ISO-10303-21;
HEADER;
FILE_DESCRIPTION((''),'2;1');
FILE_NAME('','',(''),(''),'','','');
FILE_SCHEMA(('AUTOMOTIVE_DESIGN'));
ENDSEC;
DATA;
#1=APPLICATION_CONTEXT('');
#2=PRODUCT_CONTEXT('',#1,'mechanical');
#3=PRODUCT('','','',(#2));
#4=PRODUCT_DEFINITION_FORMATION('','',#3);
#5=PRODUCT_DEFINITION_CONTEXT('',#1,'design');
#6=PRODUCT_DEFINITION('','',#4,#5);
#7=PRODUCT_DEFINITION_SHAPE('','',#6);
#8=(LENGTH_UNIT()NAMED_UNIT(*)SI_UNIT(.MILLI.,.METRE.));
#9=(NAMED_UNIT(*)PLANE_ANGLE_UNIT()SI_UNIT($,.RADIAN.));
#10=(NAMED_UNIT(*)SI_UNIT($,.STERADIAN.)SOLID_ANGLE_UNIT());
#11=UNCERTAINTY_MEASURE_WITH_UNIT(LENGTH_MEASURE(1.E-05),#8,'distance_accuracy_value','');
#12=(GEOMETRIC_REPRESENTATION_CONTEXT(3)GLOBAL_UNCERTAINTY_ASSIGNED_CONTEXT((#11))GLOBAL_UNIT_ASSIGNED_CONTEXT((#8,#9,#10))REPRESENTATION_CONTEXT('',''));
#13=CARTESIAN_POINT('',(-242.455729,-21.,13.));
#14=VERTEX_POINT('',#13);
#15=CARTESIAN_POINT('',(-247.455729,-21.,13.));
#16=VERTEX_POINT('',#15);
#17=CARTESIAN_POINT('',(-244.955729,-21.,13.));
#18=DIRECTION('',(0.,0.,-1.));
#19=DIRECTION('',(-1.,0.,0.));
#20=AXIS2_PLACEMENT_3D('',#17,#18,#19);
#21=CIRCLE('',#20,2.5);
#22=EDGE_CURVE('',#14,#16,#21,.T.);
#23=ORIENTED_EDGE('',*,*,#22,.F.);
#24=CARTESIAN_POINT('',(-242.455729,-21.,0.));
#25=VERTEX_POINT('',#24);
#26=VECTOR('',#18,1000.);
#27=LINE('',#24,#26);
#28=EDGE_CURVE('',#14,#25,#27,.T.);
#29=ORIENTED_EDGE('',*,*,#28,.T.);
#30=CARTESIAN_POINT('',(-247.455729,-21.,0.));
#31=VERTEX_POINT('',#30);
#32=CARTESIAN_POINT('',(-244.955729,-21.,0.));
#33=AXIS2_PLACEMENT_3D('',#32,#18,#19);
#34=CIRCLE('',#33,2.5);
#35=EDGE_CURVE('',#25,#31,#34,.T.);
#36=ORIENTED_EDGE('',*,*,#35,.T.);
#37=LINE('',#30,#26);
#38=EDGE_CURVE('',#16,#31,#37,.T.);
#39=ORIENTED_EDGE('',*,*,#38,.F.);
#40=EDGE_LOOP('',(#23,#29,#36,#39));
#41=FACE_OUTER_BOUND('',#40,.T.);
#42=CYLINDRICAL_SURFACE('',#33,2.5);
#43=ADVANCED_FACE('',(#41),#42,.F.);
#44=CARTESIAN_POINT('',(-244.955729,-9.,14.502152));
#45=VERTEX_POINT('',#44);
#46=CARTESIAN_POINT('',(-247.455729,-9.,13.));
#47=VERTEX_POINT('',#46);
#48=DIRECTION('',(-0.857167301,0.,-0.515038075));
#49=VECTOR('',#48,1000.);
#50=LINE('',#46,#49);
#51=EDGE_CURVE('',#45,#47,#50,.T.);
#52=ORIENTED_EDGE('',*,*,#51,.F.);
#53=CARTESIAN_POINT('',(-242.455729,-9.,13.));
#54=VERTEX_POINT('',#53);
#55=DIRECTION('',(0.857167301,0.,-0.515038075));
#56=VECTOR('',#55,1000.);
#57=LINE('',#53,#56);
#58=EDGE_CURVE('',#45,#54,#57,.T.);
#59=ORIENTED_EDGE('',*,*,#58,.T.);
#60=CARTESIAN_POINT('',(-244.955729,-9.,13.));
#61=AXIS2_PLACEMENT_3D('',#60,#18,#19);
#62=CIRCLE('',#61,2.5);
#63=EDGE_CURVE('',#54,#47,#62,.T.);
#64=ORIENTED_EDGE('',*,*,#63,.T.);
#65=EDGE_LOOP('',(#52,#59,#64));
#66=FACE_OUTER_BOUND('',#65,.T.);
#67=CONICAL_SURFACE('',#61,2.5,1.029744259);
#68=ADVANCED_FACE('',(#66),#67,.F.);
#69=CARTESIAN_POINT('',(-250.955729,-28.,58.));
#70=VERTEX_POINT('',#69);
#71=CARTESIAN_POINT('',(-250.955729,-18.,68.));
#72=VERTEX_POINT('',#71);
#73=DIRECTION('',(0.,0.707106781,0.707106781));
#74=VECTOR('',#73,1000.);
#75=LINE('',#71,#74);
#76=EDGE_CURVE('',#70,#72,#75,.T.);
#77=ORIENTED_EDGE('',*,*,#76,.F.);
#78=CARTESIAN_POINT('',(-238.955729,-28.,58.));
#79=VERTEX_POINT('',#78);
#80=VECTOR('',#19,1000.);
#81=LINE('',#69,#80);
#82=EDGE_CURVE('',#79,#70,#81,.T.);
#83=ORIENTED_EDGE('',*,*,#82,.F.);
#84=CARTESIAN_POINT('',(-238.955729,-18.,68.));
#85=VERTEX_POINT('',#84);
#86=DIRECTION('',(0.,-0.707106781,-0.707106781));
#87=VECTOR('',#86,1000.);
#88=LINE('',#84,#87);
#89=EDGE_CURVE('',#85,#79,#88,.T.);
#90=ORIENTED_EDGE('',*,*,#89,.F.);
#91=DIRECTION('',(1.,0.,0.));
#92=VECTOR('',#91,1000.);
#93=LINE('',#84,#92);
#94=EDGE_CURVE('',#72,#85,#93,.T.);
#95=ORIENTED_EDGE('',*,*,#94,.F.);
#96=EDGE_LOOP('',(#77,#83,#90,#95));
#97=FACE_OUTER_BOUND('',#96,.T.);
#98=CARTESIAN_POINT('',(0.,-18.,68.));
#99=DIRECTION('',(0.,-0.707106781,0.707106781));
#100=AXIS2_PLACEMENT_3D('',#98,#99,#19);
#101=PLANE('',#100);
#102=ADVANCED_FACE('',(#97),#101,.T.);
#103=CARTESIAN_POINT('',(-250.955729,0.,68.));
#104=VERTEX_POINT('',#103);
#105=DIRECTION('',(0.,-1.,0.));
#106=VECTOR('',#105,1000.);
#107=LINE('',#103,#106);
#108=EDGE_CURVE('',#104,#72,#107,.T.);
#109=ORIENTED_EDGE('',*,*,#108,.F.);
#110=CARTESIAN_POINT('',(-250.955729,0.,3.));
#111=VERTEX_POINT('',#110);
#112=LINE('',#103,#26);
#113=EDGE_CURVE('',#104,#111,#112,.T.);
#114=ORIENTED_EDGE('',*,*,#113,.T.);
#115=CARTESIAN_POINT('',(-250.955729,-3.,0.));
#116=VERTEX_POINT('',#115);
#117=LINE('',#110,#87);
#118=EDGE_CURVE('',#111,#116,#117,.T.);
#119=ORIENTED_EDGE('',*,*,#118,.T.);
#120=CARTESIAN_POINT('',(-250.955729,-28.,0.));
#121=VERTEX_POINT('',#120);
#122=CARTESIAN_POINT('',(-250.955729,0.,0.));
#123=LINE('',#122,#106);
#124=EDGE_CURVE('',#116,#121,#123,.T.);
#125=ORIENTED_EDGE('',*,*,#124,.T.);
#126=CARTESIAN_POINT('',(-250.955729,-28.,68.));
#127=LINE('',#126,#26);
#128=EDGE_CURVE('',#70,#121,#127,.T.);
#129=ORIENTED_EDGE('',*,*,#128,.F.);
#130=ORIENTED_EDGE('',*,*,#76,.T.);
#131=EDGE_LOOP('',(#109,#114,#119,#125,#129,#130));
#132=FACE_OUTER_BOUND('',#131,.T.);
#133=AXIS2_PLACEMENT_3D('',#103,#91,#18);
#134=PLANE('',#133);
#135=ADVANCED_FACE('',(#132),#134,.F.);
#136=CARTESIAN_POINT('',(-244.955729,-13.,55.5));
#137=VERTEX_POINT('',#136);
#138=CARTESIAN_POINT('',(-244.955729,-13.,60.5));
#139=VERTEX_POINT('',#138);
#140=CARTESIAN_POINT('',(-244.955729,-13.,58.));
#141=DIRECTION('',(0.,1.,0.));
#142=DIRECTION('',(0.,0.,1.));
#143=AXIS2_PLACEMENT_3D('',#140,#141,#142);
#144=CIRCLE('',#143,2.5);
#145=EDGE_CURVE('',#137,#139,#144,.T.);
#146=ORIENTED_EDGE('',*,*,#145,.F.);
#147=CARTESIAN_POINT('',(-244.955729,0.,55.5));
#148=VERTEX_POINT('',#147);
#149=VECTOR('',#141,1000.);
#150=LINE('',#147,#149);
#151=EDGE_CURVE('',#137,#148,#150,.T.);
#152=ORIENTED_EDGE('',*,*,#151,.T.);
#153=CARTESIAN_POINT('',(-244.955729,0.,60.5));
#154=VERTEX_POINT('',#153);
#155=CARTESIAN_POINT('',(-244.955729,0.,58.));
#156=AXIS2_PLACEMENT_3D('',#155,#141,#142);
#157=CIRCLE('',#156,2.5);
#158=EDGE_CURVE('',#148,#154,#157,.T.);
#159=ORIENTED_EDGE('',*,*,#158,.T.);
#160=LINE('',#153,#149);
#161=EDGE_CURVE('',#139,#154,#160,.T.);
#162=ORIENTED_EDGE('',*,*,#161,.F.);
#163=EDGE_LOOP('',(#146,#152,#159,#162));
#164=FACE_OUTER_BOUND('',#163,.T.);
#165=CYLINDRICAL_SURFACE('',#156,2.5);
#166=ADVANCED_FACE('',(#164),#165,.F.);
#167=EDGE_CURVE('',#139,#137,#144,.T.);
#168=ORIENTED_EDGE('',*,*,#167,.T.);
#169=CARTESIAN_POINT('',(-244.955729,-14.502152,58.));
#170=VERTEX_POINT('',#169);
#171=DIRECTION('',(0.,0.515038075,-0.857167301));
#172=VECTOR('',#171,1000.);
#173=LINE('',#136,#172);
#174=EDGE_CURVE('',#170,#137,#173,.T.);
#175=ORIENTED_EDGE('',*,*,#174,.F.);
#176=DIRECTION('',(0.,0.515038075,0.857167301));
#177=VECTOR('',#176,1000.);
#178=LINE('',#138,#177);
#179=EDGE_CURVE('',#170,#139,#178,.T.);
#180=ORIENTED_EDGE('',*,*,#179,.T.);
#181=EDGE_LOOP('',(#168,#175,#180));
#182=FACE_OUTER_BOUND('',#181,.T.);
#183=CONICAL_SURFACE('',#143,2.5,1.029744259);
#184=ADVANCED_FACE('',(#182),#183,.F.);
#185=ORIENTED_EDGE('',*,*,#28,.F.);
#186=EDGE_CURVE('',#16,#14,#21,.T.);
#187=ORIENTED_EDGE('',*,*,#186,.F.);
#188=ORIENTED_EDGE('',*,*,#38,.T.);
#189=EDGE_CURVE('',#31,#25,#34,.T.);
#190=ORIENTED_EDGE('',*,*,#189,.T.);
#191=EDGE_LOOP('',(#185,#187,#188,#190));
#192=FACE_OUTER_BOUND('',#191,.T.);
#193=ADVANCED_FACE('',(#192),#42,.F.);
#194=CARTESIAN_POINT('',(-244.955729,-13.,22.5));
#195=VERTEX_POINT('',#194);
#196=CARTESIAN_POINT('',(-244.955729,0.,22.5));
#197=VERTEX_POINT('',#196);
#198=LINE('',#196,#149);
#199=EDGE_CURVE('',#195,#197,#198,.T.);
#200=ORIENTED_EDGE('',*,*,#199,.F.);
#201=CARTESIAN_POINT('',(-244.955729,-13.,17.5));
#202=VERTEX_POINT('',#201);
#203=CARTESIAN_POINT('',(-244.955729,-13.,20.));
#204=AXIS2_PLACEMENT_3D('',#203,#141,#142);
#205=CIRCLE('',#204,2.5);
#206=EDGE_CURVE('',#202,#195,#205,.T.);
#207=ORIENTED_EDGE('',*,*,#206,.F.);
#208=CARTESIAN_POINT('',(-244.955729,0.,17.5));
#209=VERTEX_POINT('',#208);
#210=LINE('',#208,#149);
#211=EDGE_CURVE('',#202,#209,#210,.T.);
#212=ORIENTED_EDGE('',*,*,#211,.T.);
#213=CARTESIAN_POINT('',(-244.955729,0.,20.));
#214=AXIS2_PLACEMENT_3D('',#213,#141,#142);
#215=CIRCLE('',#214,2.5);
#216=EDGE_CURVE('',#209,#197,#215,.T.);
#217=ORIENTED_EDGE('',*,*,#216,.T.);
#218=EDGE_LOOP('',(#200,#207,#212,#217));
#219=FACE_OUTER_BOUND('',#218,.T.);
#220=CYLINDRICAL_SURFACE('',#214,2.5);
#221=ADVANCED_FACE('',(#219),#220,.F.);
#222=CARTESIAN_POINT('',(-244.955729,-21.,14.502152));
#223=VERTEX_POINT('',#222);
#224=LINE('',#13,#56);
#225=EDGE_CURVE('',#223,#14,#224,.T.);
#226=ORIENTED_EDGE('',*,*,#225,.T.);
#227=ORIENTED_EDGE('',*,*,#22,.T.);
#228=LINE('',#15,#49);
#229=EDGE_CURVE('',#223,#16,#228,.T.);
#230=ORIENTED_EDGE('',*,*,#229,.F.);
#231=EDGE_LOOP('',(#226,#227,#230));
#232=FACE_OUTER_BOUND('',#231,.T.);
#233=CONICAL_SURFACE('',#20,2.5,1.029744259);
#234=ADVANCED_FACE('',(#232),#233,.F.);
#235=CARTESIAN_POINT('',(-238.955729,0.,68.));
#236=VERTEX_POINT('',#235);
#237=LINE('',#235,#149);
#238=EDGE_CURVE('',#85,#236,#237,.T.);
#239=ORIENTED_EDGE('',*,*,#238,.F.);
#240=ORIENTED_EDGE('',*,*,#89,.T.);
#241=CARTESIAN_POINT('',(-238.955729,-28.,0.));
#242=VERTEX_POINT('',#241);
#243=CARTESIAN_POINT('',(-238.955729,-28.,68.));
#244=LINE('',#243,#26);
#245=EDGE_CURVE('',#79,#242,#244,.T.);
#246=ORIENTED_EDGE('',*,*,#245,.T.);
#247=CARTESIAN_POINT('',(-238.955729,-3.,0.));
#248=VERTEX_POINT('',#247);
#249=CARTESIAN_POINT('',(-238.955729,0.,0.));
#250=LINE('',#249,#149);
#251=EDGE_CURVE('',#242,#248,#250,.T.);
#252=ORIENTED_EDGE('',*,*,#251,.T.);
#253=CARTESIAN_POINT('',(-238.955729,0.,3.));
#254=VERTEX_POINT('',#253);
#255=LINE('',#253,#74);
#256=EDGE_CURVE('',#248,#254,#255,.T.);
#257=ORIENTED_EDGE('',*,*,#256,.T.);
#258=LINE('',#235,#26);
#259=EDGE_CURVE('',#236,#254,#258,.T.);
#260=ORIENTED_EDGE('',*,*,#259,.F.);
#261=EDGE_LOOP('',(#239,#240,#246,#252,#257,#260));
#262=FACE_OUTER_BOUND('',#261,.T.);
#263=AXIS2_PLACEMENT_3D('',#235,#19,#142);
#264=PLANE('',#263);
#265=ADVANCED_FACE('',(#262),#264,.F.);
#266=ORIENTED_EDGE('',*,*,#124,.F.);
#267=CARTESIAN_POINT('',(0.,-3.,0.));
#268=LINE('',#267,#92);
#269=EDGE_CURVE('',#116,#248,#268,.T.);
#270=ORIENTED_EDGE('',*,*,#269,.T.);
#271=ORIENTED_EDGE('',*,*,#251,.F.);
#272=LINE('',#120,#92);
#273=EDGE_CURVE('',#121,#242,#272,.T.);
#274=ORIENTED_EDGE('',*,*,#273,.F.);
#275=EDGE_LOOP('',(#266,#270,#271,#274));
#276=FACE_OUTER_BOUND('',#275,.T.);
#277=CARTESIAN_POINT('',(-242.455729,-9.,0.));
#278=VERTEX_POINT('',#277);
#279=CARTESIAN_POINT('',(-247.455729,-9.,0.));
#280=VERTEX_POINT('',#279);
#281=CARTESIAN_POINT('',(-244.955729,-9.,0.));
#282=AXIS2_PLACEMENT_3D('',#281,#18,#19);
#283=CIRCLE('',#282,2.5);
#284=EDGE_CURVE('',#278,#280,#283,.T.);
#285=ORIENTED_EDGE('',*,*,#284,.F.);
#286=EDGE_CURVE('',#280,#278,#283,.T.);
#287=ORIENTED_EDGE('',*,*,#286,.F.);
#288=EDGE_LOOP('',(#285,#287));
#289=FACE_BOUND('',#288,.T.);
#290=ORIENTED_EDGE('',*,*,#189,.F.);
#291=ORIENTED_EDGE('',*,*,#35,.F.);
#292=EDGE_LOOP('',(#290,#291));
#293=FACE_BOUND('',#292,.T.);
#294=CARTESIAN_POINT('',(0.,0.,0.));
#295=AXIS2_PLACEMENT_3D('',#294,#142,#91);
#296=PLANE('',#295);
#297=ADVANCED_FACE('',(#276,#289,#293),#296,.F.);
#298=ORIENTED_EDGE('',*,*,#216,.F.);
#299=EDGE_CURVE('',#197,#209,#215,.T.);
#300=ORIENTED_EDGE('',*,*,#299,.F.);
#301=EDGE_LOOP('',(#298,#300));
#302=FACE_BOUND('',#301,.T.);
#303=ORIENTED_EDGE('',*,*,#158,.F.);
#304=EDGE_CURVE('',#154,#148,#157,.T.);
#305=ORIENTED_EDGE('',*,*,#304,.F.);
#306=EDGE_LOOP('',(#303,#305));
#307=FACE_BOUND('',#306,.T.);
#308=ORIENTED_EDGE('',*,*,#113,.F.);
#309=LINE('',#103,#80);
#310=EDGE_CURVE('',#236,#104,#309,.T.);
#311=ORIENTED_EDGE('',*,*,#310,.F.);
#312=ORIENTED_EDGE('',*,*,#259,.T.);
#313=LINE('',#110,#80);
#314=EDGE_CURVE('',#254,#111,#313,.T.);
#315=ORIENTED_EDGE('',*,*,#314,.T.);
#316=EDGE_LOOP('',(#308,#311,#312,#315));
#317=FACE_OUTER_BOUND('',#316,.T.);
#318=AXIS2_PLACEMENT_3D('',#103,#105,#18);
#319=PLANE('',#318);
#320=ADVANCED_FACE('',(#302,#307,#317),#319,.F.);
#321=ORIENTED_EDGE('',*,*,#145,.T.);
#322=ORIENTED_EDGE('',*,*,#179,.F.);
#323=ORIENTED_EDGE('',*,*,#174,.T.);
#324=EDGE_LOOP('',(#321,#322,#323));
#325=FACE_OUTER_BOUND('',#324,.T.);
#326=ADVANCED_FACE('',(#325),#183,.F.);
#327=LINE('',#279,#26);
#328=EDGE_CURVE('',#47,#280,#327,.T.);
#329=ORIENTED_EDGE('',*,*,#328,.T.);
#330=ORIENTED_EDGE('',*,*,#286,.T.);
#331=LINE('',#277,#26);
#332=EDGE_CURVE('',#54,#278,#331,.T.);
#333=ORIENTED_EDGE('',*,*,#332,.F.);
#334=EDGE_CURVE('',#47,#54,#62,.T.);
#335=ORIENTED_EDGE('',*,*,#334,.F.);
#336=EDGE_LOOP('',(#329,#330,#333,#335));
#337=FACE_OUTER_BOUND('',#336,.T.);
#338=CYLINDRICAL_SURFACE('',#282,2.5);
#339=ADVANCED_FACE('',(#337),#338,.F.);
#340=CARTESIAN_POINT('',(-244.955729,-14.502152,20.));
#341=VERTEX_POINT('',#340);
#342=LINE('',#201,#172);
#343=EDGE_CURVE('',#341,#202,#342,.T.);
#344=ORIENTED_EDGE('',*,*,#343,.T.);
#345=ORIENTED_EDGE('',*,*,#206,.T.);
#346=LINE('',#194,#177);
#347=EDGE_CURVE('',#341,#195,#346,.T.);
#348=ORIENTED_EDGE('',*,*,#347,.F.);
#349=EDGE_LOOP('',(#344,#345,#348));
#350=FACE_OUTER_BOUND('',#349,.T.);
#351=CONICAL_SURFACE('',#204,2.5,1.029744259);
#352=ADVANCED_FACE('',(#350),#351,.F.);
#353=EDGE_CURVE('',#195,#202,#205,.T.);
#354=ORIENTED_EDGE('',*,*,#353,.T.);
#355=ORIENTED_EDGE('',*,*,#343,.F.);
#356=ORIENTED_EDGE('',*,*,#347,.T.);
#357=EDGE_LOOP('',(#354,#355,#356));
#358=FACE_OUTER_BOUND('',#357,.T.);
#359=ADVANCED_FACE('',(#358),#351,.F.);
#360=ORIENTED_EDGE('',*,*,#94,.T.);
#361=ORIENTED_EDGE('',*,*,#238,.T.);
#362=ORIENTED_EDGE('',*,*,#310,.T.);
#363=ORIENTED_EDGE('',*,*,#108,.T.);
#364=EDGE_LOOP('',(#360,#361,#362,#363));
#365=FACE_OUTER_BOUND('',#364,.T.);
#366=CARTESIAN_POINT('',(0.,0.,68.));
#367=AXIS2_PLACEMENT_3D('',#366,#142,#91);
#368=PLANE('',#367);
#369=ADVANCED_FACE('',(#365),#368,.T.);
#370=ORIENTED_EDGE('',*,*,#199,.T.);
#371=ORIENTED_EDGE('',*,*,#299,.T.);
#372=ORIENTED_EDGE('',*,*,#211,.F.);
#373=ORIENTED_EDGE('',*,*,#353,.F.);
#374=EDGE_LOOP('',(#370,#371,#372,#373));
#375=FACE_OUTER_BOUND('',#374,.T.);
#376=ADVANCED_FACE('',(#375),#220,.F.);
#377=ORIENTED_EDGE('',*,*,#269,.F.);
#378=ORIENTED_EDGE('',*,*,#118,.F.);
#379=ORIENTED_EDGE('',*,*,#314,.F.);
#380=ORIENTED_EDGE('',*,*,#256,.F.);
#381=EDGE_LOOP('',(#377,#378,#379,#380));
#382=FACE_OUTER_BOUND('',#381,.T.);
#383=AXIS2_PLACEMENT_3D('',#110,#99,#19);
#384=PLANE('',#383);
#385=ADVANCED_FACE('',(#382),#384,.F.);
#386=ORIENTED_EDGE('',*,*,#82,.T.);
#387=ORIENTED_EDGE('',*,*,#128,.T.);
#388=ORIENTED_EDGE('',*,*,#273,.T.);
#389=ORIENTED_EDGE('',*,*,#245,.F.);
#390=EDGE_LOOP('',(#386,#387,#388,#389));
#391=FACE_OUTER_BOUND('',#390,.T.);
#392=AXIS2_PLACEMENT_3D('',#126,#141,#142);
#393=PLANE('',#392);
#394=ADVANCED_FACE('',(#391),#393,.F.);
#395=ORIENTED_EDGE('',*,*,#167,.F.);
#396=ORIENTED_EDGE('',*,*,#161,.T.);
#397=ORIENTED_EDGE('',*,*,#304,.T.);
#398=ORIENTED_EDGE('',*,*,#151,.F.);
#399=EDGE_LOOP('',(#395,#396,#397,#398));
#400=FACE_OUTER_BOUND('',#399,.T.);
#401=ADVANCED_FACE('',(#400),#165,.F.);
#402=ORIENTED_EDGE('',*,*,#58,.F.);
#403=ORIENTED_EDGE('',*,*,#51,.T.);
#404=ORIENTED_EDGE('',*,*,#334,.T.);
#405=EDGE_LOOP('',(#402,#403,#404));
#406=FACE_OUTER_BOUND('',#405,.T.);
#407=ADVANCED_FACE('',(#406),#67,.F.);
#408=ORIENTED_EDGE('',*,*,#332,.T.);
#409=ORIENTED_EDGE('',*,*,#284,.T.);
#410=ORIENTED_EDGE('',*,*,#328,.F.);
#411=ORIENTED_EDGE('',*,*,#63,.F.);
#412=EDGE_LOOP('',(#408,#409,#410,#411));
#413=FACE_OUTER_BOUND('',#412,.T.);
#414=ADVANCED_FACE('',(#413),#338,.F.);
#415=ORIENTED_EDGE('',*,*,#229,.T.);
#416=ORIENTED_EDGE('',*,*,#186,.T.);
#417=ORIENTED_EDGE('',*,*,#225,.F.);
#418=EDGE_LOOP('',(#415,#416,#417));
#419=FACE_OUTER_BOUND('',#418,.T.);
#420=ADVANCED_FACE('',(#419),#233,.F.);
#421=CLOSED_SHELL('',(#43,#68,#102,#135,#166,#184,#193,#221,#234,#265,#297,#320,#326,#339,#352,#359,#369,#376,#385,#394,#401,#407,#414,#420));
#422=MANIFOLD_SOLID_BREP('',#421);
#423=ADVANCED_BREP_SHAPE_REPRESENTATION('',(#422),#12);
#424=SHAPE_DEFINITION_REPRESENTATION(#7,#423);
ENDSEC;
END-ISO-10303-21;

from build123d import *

# Parameters (mm, degrees)
SKETCH_1_W             = 12
SKETCH_1_H             = 28
EXTRUDE_1_DEPTH        = 68
CHAMFER_1_SIZE         = 10
CHAMFER_2_SIZE         = 3
HOLE_WIZARD_M6_1_D     = 5
HOLE_WIZARD_M6_1_DEPTH = 13
HOLE_WIZARD_M6_1_TIP   = 1.502151548
HOLE_WIZARD_M6_2_D     = 5
HOLE_WIZARD_M6_2_DEPTH = 13
HOLE_WIZARD_M6_2_TIP   = 1.502151548


with BuildPart() as part:
    # 草图1 → 凸台-拉伸1 (new body)
    with BuildSketch(Plane.XY):
        with Locations((-244.955728906, -14)):
            Rectangle(SKETCH_1_W, SKETCH_1_H)
    extrude(amount=EXTRUDE_1_DEPTH)

    # 倒角1
    chamfer_1_edges = [part.edges().sort_by_distance(p)[0] for p in [
        (-244.955728906, -28, 68),
    ]]
    chamfer(chamfer_1_edges, length=CHAMFER_1_SIZE)

    # 倒角2
    chamfer_2_edges = [part.edges().sort_by_distance(p)[0] for p in [
        (-244.955728906, 0, 0),
    ]]
    chamfer(chamfer_2_edges, length=CHAMFER_2_SIZE)

    # M6 螺纹孔1
    with Locations(Plane(origin=(0, 0, 0), x_dir=(-1, 0, 0), z_dir=(0, 0, -1))):
        with Locations((244.955728906, -9), (244.955728906, -21)):
            Hole(HOLE_WIZARD_M6_1_D / 2, depth=HOLE_WIZARD_M6_1_DEPTH)
            with Locations((0, 0, -(HOLE_WIZARD_M6_1_DEPTH + HOLE_WIZARD_M6_1_TIP / 2))):  # 118° drill point
                Cone(0, HOLE_WIZARD_M6_1_D / 2, HOLE_WIZARD_M6_1_TIP, mode=Mode.SUBTRACT)

    # M6 螺纹孔2
    with Locations(Plane(origin=(0, 0, 0), x_dir=(1, 0, 0), z_dir=(0, 1, 0))):
        with Locations((-244.955728906, -58), (-244.955728906, -20)):
            Hole(HOLE_WIZARD_M6_2_D / 2, depth=HOLE_WIZARD_M6_2_DEPTH)
            with Locations((0, 0, -(HOLE_WIZARD_M6_2_DEPTH + HOLE_WIZARD_M6_2_TIP / 2))):  # 118° drill point
                Cone(0, HOLE_WIZARD_M6_2_D / 2, HOLE_WIZARD_M6_2_TIP, mode=Mode.SUBTRACT)


solid = part.part
